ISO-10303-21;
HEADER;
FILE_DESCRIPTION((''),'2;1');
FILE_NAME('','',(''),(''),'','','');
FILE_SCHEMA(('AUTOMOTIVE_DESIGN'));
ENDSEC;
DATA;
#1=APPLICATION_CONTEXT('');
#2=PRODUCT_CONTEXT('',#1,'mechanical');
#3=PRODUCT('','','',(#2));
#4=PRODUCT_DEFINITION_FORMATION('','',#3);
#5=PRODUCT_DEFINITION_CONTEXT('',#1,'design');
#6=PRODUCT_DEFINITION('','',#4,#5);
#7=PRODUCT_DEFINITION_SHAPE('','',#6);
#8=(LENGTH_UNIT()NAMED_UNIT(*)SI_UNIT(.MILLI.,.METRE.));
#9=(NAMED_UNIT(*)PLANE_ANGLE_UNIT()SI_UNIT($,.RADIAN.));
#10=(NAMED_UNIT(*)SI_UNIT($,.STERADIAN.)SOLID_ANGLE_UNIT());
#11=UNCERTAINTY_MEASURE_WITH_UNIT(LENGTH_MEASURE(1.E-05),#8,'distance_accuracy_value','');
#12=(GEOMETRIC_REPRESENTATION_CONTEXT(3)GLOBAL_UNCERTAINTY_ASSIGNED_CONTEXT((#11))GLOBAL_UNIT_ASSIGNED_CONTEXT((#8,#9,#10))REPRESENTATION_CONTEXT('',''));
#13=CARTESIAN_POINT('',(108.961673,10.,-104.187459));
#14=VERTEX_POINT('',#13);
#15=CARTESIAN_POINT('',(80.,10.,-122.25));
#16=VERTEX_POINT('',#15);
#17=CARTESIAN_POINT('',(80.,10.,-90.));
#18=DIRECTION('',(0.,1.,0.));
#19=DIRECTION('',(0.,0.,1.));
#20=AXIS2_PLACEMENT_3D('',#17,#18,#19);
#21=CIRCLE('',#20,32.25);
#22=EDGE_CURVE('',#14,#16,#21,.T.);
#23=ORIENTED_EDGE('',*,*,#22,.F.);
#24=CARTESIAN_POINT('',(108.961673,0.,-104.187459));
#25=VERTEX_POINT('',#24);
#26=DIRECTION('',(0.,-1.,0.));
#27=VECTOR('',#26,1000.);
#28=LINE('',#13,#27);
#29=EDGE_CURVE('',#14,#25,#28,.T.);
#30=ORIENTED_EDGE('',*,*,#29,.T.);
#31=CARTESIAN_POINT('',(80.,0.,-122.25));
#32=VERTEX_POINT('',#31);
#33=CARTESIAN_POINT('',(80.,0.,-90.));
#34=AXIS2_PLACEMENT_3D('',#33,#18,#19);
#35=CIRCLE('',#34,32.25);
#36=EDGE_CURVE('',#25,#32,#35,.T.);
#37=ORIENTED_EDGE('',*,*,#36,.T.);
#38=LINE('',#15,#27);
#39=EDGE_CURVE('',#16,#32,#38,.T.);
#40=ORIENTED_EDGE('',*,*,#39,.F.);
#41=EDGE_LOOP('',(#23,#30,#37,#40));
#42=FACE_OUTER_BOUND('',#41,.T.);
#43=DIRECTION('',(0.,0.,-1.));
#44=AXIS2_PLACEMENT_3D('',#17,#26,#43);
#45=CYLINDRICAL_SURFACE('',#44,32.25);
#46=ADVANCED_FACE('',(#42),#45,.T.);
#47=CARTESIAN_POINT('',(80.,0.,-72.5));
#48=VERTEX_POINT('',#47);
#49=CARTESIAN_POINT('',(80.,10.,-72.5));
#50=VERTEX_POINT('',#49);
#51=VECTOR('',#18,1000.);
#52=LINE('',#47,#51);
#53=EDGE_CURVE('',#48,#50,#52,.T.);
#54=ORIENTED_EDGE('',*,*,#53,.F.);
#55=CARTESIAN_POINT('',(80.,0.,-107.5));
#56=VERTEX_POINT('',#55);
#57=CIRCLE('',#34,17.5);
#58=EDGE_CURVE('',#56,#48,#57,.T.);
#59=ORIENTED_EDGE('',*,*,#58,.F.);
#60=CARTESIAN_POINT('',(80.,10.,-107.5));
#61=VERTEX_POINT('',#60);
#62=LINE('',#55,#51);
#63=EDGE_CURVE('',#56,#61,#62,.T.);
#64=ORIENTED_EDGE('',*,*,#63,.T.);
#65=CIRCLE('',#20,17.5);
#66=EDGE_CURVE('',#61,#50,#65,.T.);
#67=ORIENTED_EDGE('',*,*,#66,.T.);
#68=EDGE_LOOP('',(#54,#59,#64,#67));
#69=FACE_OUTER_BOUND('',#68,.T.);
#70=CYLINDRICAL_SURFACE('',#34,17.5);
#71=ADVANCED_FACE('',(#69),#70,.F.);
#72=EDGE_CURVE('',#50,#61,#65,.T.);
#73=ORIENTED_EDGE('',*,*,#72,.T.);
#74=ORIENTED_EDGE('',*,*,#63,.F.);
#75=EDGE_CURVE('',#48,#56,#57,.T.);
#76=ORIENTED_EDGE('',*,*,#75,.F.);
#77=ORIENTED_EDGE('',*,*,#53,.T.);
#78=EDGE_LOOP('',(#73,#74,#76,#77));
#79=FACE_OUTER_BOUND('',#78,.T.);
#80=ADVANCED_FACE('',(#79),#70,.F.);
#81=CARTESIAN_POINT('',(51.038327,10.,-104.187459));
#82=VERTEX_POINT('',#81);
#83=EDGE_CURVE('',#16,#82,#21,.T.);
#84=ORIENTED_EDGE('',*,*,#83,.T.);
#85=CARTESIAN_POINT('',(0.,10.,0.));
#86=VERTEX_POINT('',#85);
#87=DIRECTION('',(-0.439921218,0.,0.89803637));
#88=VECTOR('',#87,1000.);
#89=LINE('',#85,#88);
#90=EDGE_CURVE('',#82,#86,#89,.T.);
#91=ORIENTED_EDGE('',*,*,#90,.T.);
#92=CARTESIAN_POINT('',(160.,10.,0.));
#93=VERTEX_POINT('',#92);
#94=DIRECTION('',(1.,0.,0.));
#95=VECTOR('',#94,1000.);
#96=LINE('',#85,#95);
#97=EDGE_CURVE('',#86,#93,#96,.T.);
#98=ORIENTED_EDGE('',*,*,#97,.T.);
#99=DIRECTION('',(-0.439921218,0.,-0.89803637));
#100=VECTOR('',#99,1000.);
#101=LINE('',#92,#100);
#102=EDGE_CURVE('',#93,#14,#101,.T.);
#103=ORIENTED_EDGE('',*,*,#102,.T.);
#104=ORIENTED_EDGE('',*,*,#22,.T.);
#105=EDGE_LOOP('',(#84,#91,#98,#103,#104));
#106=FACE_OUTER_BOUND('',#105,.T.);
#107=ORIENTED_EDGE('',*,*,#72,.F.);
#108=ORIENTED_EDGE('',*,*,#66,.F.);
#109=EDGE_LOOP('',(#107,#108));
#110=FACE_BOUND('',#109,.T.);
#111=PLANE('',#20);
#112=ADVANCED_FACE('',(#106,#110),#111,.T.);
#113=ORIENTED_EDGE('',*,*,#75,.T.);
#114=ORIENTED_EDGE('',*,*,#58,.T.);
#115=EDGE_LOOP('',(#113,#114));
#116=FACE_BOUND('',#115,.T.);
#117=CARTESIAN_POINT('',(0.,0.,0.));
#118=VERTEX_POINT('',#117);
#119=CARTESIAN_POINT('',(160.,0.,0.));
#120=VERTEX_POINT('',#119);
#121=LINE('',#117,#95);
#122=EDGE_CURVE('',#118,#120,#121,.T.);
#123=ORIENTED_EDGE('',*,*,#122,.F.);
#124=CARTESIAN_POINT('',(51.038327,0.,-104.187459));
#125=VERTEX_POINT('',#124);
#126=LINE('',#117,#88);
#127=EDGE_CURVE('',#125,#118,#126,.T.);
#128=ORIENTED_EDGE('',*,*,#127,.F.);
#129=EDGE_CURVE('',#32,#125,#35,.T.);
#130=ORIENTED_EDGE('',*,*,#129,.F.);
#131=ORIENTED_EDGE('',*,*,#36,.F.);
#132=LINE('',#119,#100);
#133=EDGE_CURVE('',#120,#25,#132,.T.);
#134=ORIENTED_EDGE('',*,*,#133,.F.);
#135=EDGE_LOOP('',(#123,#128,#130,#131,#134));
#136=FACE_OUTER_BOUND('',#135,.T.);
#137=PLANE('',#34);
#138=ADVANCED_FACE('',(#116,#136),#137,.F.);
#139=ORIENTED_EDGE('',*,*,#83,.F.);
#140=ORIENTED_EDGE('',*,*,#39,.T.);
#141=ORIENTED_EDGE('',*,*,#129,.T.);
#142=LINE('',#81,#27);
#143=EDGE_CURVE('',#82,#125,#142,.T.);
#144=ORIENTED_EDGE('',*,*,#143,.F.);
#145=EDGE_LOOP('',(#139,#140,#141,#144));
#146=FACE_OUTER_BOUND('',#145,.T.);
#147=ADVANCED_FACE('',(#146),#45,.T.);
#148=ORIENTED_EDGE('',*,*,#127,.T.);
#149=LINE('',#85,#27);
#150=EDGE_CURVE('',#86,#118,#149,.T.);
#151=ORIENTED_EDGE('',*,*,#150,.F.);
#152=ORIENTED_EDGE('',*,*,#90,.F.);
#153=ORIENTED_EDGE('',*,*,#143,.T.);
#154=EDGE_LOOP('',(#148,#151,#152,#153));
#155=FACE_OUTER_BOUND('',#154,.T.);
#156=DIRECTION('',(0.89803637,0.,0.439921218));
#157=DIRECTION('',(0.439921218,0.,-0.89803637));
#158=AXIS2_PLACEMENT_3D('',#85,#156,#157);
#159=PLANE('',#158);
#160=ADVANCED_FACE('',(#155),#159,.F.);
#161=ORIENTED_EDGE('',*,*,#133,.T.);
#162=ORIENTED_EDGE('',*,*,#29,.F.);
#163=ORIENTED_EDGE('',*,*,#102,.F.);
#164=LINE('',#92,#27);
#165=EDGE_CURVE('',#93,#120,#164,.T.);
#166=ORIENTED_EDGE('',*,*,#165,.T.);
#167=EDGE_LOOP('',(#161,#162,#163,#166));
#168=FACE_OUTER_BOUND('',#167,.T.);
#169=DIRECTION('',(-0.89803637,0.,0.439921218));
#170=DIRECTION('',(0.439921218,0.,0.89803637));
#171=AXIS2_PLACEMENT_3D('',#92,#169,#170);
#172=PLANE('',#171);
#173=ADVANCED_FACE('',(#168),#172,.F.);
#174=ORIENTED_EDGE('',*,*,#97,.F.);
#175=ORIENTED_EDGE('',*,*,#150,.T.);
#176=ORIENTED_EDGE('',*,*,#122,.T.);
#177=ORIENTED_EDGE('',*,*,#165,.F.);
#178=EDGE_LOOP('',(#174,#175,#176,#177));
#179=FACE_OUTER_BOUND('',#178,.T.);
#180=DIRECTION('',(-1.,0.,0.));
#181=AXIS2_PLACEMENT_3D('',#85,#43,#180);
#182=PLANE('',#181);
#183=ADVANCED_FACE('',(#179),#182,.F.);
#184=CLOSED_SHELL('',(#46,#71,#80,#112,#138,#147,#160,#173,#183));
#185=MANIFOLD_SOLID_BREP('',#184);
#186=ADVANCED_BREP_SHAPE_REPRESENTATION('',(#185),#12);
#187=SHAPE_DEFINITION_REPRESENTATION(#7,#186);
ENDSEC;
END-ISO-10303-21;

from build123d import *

# Parameters (mm, degrees)
SKETCH_1_R          = 17.25
EXTRUDE_1_DEPTH     = 10
SKETCH_2_R          = 17.5
CUT_EXTRUDE_1_DEPTH = 10


with BuildPart() as part:
    # 草图1 → 凸台-拉伸1 (new body)
    with BuildSketch(Plane(origin=(0, 0, 0), x_dir=(1, 0, 0), z_dir=(0, 1, 0))):
        with BuildLine():
            Line((0, 0), (160, 0))
            Line((160, 0), (108.961672936, 104.187459277))
            ThreePointArc((108.961672936, 104.187459277), (80, 122.25), (51.038327064, 104.187459277))
            Line((51.038327064, 104.187459277), (0, 0))
        make_face()
        with Locations(Location((80, 90, 0), (0, 0, 270))):
            Circle(SKETCH_1_R, mode=Mode.SUBTRACT)
    extrude(amount=EXTRUDE_1_DEPTH)

    # 草图2 → 切除-拉伸1 (cut)
    with BuildSketch(Plane(origin=(0, 10, 0), x_dir=(1, 0, 0), z_dir=(0, 1, 0))):
        with Locations(Location((80, 90, 0), (0, 0, 270))):
            Circle(SKETCH_2_R)
    extrude(amount=-CUT_EXTRUDE_1_DEPTH, mode=Mode.SUBTRACT)


solid = part.part
